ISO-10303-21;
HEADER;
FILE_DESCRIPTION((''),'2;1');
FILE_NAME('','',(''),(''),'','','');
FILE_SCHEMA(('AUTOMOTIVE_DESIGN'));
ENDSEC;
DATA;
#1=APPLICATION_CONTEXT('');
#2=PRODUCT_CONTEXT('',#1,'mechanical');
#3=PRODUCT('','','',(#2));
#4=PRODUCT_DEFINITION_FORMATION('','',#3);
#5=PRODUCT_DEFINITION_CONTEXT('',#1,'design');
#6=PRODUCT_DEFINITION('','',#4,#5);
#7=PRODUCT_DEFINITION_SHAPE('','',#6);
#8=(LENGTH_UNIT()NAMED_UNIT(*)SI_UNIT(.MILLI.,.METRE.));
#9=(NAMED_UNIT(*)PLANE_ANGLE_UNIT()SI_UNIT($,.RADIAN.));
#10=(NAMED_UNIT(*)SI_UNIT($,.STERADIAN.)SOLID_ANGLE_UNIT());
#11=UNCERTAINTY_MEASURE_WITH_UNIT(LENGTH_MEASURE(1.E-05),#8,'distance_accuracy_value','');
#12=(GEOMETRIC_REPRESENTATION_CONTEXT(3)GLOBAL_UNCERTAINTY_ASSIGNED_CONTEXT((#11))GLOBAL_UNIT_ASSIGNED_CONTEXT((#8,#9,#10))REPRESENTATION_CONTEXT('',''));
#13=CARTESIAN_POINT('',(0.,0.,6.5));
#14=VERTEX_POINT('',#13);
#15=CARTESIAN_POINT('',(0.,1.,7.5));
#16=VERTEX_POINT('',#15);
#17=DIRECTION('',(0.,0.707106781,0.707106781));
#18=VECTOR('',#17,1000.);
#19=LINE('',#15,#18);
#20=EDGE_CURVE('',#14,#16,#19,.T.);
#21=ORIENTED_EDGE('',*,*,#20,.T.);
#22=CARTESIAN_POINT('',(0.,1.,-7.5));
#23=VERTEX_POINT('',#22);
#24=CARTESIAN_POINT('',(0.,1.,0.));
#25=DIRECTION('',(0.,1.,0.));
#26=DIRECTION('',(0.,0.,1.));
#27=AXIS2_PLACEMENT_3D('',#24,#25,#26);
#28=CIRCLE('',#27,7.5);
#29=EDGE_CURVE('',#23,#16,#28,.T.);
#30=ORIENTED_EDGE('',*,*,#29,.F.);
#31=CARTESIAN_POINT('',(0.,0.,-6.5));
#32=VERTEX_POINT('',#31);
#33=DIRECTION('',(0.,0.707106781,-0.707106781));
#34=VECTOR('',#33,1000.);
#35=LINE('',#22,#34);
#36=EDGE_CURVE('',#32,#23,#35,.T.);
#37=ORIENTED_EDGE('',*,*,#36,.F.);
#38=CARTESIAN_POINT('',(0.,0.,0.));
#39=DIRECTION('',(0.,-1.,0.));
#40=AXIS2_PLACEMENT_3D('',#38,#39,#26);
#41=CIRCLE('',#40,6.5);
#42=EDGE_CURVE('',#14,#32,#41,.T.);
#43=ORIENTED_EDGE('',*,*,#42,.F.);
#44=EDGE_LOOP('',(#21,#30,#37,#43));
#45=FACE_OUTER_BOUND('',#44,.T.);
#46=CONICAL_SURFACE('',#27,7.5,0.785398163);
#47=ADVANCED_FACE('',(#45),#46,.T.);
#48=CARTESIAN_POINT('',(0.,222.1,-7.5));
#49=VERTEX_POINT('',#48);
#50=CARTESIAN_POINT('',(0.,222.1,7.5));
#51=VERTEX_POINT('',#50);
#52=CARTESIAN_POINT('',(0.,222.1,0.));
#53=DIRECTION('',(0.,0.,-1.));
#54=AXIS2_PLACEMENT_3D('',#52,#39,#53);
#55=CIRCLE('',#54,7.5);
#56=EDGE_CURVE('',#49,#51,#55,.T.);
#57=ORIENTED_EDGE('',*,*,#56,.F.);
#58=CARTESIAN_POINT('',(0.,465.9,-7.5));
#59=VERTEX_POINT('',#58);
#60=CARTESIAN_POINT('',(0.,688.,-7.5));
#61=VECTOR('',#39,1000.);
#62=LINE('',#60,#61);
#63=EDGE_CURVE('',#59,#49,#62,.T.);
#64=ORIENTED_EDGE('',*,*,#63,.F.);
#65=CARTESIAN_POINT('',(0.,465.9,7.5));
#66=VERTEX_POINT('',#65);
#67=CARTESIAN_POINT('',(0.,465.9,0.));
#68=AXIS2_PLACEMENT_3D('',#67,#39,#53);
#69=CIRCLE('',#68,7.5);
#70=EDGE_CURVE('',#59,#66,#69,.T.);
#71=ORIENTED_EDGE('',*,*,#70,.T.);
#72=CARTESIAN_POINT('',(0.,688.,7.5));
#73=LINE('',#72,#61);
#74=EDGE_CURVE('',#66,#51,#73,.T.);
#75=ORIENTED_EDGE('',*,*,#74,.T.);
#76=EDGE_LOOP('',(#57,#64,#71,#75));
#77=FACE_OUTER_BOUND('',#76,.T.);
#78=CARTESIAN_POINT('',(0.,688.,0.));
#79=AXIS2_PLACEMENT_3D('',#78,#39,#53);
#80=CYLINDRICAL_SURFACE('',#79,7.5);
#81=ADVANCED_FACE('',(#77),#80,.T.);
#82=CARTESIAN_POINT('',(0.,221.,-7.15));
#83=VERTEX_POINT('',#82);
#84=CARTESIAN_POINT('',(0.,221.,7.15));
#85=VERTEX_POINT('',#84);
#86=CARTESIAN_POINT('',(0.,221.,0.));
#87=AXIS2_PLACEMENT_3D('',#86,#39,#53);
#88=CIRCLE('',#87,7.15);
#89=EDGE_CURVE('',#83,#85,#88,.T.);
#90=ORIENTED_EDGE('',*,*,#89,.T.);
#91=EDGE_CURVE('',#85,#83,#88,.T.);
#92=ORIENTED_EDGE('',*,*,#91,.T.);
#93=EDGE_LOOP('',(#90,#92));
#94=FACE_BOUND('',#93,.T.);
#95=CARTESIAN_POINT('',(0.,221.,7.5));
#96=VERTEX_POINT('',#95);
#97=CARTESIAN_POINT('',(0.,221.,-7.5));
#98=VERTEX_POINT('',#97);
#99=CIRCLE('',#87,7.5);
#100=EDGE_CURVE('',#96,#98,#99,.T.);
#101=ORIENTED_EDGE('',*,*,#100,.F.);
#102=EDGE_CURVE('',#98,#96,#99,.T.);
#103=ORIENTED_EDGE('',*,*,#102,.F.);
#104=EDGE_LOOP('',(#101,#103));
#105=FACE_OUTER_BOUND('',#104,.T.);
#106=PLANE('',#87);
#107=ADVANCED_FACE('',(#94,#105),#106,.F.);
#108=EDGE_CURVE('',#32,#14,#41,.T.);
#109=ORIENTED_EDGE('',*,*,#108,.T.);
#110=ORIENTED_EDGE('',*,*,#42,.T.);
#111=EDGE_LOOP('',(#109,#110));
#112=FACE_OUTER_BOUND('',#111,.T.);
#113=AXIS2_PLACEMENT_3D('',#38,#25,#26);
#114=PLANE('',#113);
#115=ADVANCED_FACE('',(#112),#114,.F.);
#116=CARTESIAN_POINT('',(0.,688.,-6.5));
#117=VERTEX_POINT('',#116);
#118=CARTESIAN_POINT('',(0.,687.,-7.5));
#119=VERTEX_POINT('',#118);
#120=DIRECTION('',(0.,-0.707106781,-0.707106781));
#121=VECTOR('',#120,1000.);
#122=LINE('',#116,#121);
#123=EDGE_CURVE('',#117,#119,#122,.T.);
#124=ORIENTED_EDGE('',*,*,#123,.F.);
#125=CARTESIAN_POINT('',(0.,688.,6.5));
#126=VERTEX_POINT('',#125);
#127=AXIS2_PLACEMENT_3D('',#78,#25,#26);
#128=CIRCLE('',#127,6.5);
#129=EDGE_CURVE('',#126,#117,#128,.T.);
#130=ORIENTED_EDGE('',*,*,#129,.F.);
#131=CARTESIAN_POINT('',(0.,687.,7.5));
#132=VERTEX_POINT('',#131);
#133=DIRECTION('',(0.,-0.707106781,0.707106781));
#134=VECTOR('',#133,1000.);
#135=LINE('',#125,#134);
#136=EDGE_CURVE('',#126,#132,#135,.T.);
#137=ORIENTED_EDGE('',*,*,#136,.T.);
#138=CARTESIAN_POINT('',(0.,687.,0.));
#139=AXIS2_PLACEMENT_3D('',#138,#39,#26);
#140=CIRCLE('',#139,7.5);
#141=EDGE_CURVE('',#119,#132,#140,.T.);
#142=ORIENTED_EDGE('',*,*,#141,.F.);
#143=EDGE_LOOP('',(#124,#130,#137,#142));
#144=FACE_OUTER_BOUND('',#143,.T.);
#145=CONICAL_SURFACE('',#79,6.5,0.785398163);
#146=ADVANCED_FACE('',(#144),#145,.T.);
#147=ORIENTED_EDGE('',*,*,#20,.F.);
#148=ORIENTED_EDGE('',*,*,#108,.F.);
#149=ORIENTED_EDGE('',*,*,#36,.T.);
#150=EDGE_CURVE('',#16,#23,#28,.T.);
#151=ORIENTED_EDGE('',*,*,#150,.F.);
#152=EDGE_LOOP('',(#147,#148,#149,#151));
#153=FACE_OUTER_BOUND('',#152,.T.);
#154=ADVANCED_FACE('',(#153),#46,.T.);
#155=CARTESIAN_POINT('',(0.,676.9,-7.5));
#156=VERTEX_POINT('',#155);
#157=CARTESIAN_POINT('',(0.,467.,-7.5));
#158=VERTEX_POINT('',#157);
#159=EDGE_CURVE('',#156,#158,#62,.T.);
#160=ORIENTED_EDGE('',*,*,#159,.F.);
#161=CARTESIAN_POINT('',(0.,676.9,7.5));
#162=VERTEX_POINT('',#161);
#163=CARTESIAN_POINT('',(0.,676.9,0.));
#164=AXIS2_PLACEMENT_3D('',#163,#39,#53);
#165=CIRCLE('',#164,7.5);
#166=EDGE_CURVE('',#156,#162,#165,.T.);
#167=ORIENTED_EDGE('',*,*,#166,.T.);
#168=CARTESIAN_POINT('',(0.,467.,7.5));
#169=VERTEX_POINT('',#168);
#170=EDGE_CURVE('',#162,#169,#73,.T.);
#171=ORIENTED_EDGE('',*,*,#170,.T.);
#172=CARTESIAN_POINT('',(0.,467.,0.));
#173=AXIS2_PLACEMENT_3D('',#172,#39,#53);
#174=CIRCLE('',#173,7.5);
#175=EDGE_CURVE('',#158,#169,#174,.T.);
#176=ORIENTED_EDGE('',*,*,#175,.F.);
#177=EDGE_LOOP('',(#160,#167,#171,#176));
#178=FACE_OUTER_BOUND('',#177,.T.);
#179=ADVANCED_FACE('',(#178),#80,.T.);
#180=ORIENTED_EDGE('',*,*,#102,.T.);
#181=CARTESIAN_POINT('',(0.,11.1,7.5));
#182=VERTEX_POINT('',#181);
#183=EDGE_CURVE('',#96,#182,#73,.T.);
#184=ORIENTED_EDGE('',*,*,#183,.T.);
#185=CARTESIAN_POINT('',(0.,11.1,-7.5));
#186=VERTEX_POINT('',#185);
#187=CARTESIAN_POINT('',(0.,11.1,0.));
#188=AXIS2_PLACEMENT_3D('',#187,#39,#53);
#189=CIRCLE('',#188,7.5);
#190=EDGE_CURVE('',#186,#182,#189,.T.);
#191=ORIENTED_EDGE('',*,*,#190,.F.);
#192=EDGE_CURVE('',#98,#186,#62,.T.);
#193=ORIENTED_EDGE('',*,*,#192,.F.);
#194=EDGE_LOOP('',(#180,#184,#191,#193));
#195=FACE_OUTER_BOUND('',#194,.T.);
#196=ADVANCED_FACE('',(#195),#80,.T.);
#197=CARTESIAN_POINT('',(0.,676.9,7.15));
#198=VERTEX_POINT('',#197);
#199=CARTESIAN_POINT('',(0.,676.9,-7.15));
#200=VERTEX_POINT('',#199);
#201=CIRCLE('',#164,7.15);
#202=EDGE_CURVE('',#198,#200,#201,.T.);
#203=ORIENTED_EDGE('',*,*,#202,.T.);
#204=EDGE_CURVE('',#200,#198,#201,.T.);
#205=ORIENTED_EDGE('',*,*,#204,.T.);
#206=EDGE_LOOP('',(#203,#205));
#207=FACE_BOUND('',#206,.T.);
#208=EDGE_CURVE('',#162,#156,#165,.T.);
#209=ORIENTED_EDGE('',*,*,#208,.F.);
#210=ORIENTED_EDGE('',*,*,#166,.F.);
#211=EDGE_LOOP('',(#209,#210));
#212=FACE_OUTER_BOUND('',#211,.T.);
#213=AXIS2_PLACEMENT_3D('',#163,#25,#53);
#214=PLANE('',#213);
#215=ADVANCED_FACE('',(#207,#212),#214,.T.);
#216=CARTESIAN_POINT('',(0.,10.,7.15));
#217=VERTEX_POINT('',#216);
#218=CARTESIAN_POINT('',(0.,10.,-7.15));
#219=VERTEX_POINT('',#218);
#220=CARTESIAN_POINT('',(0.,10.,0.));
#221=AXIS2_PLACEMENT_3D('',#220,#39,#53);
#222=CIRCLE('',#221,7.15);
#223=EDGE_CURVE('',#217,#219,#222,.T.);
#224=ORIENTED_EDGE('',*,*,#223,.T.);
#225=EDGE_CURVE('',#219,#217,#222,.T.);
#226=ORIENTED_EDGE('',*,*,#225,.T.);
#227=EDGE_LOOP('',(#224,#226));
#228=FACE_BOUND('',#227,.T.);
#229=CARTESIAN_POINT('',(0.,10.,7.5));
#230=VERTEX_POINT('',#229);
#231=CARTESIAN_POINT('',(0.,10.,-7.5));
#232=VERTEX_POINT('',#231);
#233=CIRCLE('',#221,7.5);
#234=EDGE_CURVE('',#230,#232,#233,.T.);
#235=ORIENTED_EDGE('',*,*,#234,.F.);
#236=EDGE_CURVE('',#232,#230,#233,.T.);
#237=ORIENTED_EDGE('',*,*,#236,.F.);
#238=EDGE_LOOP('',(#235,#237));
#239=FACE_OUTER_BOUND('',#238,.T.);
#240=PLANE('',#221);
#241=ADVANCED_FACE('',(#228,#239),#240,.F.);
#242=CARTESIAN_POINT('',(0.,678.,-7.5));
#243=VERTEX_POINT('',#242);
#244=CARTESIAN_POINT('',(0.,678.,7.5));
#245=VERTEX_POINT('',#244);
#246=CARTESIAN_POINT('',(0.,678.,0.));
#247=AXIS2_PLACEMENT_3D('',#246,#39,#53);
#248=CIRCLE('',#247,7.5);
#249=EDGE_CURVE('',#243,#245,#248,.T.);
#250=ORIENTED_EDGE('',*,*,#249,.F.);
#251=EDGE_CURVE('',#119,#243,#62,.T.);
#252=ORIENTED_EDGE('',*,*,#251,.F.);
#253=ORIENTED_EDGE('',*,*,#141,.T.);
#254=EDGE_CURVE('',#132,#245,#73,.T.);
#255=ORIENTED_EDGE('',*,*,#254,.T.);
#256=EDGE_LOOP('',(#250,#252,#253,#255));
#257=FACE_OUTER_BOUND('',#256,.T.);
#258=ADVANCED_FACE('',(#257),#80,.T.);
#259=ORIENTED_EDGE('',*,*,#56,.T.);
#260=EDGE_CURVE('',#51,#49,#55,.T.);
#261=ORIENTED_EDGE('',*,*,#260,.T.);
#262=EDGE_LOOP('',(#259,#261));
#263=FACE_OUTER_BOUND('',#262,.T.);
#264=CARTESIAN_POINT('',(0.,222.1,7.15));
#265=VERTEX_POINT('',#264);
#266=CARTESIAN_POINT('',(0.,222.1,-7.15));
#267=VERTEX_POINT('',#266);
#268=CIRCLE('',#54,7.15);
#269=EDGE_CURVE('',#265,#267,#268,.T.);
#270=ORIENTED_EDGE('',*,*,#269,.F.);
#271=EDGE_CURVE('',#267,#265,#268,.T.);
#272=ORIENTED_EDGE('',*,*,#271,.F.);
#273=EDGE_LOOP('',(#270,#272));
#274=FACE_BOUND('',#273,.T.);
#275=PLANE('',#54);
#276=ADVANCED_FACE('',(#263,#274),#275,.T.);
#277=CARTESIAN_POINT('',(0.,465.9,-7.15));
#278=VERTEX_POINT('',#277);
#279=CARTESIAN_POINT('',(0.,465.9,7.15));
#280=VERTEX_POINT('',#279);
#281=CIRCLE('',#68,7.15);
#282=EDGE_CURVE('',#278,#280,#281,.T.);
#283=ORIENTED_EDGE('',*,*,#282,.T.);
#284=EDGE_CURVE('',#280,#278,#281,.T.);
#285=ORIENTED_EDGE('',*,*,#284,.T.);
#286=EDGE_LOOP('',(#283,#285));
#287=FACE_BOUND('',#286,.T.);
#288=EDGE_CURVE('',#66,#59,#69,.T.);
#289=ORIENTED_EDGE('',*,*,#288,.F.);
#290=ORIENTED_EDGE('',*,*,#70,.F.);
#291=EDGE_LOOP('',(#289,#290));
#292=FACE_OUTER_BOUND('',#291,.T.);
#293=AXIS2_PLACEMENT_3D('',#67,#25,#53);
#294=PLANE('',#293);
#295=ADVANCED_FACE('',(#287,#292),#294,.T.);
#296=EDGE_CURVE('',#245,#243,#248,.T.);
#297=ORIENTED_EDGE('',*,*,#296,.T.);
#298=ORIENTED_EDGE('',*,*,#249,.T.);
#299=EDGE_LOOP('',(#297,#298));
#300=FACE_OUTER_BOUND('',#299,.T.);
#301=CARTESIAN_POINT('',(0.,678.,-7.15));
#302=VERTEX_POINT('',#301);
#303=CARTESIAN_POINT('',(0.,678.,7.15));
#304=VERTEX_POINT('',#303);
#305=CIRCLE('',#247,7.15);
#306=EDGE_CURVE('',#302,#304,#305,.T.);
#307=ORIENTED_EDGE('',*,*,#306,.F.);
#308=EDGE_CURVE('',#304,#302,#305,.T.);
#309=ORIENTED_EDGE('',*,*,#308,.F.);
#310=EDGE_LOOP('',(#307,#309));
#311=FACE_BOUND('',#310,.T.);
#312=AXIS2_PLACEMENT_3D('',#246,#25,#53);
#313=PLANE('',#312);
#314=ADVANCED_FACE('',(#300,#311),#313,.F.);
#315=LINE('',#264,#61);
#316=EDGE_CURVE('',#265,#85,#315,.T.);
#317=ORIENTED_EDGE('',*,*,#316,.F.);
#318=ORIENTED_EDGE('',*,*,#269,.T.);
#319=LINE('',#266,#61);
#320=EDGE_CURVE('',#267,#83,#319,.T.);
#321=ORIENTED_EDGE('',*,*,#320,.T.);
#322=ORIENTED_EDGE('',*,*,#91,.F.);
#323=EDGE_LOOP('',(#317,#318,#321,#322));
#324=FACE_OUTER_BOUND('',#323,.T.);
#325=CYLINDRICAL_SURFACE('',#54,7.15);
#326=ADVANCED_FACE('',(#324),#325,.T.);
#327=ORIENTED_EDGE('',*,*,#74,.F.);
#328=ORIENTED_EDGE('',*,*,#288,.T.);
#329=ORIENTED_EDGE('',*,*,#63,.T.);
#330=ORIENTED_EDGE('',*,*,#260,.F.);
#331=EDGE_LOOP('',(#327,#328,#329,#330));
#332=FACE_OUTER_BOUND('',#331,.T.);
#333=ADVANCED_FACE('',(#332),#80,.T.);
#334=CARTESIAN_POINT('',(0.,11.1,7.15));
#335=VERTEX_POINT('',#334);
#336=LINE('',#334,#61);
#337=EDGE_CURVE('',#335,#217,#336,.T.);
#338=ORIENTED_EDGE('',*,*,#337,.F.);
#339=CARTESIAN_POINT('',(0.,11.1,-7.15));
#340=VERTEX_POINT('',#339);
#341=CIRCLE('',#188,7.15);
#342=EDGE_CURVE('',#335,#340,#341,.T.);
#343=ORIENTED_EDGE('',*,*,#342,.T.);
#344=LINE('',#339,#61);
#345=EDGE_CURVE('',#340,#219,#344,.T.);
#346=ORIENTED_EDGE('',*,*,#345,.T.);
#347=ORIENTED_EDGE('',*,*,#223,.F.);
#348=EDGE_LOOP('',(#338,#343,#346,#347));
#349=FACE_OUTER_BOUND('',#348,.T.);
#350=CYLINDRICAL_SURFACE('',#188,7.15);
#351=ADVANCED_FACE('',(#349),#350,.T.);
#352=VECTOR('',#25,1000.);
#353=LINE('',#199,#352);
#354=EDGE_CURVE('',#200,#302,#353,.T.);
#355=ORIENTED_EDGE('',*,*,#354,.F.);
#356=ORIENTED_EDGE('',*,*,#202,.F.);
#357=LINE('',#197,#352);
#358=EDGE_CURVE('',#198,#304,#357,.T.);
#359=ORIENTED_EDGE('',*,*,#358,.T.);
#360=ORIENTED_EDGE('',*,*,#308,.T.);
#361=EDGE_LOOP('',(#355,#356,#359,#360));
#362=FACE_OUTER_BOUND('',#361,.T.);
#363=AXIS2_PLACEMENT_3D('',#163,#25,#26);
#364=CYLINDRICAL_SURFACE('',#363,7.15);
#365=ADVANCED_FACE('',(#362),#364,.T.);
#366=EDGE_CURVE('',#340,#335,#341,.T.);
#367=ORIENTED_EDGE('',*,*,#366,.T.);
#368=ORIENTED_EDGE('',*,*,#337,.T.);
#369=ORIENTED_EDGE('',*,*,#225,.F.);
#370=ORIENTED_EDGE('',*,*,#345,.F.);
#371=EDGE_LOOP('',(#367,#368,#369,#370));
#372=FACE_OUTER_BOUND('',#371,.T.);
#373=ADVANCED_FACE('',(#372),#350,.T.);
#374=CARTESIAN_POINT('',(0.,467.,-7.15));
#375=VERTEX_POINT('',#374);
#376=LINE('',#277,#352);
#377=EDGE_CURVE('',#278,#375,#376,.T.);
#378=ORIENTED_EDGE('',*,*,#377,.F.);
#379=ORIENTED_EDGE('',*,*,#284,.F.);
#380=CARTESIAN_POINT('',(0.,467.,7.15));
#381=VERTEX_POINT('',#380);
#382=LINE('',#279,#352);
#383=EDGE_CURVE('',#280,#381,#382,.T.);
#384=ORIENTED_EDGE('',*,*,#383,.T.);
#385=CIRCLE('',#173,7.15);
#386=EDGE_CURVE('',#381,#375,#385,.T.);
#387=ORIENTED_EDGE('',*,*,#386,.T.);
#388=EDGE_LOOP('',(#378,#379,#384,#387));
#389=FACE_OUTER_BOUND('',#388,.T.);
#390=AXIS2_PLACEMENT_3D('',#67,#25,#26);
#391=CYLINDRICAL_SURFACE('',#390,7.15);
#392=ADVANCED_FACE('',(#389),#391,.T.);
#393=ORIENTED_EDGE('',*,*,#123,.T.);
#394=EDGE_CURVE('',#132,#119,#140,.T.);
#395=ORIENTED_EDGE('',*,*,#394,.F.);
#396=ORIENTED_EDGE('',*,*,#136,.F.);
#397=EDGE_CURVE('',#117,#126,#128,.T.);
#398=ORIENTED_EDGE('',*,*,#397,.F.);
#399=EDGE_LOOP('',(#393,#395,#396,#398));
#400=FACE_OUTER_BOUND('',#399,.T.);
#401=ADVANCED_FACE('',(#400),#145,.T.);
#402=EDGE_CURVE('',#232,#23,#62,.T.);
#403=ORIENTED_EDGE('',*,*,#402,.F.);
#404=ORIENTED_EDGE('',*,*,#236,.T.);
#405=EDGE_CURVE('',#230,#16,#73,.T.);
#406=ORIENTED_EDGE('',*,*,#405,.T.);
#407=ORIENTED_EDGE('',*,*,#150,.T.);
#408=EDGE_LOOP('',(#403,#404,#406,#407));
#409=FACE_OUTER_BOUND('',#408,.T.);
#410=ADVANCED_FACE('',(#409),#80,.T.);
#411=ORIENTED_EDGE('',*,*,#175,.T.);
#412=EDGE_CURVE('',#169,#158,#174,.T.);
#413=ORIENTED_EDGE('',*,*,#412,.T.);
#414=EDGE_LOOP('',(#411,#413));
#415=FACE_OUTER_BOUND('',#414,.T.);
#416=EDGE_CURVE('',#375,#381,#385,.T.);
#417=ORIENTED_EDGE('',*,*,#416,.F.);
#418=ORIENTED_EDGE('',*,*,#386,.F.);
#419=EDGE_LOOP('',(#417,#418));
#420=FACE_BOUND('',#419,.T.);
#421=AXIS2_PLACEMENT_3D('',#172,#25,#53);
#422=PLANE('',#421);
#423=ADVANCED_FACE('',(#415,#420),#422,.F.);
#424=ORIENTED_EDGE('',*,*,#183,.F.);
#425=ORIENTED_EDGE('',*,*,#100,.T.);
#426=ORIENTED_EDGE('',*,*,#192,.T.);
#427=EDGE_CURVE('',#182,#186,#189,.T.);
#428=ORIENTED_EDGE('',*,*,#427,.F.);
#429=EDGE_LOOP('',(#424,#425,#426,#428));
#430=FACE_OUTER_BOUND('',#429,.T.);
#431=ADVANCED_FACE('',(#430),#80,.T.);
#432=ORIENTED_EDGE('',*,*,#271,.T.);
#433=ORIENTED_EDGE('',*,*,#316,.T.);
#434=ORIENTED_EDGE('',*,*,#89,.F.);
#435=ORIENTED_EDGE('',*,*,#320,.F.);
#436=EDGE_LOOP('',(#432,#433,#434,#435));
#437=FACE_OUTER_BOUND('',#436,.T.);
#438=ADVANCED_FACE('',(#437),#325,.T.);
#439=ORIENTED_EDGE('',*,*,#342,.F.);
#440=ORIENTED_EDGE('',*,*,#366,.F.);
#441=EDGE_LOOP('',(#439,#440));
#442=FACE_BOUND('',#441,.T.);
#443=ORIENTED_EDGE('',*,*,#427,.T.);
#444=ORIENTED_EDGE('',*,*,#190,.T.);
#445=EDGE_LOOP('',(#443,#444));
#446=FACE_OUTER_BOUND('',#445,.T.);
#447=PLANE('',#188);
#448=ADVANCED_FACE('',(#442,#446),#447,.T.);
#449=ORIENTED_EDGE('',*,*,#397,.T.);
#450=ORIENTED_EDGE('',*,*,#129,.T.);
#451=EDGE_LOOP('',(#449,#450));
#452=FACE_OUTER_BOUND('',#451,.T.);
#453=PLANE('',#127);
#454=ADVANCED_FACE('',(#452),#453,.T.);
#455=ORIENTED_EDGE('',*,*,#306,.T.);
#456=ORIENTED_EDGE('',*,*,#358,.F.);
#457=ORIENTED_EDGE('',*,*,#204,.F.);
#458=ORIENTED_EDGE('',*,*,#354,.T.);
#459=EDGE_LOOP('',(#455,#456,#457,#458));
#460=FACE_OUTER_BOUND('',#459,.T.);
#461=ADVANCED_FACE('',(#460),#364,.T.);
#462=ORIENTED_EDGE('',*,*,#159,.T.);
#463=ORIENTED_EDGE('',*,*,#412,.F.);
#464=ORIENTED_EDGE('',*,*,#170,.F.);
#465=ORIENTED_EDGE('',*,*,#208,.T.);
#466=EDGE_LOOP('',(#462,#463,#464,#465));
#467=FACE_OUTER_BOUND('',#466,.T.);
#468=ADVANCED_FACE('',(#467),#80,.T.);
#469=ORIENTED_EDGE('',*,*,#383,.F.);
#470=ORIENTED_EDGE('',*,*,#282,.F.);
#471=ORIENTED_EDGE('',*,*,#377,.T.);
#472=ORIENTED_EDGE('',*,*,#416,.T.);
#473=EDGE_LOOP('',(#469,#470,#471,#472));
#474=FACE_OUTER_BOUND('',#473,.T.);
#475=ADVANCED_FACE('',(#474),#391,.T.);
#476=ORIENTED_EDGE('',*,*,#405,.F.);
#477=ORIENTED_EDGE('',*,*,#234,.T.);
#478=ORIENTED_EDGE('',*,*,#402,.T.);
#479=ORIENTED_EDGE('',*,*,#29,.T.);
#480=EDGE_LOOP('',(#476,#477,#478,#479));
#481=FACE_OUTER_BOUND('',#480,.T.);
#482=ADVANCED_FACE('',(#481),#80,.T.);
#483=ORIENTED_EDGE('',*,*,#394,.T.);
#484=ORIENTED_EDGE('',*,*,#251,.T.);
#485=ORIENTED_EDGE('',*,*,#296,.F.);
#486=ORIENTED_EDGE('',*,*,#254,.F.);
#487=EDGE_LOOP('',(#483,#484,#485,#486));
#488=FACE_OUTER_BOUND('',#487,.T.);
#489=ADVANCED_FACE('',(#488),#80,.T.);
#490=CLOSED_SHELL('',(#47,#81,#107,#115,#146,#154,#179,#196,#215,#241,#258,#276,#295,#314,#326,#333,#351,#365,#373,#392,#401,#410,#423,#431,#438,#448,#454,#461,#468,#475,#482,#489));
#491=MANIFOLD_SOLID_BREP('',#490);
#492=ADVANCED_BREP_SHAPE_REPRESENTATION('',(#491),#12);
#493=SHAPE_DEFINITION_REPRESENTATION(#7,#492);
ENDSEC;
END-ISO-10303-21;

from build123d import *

# Parameters (mm, degrees)
SKETCH1_R           = 7.5
BOSS_EXTRUDE1_DEPTH = 688
SKETCH2_R           = 7.5
SKETCH2_R_2         = 7.15
CUT_EXTRUDE1_DEPTH  = 1.1
CHAMFER1_SIZE       = 1
SKETCH3_R           = 7.5
SKETCH3_R_2         = 7.15
CUT_EXTRUDE2_DEPTH  = 1.1


with BuildPart() as part:
    # Sketch1 → Boss-Extrude1 (new body)
    with BuildSketch(Plane(origin=(0, 0, 0), x_dir=(1, 0, 0), z_dir=(0, 1, 0))):
        with Locations(Location((0, 0, 0), (0, 0, 270))):
            Circle(SKETCH1_R)
    extrude(amount=BOSS_EXTRUDE1_DEPTH)

    # Sketch2 → Cut-Extrude1 (cut)
    with BuildSketch(Plane(origin=(0, 10, 0), x_dir=(-1, 0, 0), z_dir=(0, -1, 0))):
        with Locations(Location((0, 0, 0), (0, 0, 90))):
            Circle(SKETCH2_R)
        with Locations(Location((0, 0, 0), (0, 0, 90))):
            Circle(SKETCH2_R_2, mode=Mode.SUBTRACT)
    cut_extrude1 = extrude(amount=-CUT_EXTRUDE1_DEPTH, mode=Mode.SUBTRACT)

    # Chamfer1
    chamfer1_edges = [part.edges().sort_by_distance(p)[0] for p in [
        (0, 0, -7.5),
        (0, 688, -7.5),
    ]]
    chamfer(chamfer1_edges, length=CHAMFER1_SIZE)

    # Sketch3 → Cut-Extrude2 (cut)
    with BuildSketch(Plane(origin=(0, 221, 0), x_dir=(-1, 0, 0), z_dir=(0, -1, 0))):
        with Locations(Location((0, 0, 0), (0, 0, 90))):
            Circle(SKETCH3_R)
        with Locations(Location((0, 0, 0), (0, 0, 90))):
            Circle(SKETCH3_R_2, mode=Mode.SUBTRACT)
    cut_extrude2 = extrude(amount=-CUT_EXTRUDE2_DEPTH, mode=Mode.SUBTRACT)

    # Mirror1: Cut-Extrude1, Cut-Extrude2 across plane
    add(cut_extrude1.mirror(Plane(origin=(0, 344, 0), x_dir=(0, 0, 1), z_dir=(0, -1, 0))), mode=Mode.SUBTRACT)
    add(cut_extrude2.mirror(Plane(origin=(0, 344, 0), x_dir=(0, 0, 1), z_dir=(0, -1, 0))), mode=Mode.SUBTRACT)


solid = part.part
